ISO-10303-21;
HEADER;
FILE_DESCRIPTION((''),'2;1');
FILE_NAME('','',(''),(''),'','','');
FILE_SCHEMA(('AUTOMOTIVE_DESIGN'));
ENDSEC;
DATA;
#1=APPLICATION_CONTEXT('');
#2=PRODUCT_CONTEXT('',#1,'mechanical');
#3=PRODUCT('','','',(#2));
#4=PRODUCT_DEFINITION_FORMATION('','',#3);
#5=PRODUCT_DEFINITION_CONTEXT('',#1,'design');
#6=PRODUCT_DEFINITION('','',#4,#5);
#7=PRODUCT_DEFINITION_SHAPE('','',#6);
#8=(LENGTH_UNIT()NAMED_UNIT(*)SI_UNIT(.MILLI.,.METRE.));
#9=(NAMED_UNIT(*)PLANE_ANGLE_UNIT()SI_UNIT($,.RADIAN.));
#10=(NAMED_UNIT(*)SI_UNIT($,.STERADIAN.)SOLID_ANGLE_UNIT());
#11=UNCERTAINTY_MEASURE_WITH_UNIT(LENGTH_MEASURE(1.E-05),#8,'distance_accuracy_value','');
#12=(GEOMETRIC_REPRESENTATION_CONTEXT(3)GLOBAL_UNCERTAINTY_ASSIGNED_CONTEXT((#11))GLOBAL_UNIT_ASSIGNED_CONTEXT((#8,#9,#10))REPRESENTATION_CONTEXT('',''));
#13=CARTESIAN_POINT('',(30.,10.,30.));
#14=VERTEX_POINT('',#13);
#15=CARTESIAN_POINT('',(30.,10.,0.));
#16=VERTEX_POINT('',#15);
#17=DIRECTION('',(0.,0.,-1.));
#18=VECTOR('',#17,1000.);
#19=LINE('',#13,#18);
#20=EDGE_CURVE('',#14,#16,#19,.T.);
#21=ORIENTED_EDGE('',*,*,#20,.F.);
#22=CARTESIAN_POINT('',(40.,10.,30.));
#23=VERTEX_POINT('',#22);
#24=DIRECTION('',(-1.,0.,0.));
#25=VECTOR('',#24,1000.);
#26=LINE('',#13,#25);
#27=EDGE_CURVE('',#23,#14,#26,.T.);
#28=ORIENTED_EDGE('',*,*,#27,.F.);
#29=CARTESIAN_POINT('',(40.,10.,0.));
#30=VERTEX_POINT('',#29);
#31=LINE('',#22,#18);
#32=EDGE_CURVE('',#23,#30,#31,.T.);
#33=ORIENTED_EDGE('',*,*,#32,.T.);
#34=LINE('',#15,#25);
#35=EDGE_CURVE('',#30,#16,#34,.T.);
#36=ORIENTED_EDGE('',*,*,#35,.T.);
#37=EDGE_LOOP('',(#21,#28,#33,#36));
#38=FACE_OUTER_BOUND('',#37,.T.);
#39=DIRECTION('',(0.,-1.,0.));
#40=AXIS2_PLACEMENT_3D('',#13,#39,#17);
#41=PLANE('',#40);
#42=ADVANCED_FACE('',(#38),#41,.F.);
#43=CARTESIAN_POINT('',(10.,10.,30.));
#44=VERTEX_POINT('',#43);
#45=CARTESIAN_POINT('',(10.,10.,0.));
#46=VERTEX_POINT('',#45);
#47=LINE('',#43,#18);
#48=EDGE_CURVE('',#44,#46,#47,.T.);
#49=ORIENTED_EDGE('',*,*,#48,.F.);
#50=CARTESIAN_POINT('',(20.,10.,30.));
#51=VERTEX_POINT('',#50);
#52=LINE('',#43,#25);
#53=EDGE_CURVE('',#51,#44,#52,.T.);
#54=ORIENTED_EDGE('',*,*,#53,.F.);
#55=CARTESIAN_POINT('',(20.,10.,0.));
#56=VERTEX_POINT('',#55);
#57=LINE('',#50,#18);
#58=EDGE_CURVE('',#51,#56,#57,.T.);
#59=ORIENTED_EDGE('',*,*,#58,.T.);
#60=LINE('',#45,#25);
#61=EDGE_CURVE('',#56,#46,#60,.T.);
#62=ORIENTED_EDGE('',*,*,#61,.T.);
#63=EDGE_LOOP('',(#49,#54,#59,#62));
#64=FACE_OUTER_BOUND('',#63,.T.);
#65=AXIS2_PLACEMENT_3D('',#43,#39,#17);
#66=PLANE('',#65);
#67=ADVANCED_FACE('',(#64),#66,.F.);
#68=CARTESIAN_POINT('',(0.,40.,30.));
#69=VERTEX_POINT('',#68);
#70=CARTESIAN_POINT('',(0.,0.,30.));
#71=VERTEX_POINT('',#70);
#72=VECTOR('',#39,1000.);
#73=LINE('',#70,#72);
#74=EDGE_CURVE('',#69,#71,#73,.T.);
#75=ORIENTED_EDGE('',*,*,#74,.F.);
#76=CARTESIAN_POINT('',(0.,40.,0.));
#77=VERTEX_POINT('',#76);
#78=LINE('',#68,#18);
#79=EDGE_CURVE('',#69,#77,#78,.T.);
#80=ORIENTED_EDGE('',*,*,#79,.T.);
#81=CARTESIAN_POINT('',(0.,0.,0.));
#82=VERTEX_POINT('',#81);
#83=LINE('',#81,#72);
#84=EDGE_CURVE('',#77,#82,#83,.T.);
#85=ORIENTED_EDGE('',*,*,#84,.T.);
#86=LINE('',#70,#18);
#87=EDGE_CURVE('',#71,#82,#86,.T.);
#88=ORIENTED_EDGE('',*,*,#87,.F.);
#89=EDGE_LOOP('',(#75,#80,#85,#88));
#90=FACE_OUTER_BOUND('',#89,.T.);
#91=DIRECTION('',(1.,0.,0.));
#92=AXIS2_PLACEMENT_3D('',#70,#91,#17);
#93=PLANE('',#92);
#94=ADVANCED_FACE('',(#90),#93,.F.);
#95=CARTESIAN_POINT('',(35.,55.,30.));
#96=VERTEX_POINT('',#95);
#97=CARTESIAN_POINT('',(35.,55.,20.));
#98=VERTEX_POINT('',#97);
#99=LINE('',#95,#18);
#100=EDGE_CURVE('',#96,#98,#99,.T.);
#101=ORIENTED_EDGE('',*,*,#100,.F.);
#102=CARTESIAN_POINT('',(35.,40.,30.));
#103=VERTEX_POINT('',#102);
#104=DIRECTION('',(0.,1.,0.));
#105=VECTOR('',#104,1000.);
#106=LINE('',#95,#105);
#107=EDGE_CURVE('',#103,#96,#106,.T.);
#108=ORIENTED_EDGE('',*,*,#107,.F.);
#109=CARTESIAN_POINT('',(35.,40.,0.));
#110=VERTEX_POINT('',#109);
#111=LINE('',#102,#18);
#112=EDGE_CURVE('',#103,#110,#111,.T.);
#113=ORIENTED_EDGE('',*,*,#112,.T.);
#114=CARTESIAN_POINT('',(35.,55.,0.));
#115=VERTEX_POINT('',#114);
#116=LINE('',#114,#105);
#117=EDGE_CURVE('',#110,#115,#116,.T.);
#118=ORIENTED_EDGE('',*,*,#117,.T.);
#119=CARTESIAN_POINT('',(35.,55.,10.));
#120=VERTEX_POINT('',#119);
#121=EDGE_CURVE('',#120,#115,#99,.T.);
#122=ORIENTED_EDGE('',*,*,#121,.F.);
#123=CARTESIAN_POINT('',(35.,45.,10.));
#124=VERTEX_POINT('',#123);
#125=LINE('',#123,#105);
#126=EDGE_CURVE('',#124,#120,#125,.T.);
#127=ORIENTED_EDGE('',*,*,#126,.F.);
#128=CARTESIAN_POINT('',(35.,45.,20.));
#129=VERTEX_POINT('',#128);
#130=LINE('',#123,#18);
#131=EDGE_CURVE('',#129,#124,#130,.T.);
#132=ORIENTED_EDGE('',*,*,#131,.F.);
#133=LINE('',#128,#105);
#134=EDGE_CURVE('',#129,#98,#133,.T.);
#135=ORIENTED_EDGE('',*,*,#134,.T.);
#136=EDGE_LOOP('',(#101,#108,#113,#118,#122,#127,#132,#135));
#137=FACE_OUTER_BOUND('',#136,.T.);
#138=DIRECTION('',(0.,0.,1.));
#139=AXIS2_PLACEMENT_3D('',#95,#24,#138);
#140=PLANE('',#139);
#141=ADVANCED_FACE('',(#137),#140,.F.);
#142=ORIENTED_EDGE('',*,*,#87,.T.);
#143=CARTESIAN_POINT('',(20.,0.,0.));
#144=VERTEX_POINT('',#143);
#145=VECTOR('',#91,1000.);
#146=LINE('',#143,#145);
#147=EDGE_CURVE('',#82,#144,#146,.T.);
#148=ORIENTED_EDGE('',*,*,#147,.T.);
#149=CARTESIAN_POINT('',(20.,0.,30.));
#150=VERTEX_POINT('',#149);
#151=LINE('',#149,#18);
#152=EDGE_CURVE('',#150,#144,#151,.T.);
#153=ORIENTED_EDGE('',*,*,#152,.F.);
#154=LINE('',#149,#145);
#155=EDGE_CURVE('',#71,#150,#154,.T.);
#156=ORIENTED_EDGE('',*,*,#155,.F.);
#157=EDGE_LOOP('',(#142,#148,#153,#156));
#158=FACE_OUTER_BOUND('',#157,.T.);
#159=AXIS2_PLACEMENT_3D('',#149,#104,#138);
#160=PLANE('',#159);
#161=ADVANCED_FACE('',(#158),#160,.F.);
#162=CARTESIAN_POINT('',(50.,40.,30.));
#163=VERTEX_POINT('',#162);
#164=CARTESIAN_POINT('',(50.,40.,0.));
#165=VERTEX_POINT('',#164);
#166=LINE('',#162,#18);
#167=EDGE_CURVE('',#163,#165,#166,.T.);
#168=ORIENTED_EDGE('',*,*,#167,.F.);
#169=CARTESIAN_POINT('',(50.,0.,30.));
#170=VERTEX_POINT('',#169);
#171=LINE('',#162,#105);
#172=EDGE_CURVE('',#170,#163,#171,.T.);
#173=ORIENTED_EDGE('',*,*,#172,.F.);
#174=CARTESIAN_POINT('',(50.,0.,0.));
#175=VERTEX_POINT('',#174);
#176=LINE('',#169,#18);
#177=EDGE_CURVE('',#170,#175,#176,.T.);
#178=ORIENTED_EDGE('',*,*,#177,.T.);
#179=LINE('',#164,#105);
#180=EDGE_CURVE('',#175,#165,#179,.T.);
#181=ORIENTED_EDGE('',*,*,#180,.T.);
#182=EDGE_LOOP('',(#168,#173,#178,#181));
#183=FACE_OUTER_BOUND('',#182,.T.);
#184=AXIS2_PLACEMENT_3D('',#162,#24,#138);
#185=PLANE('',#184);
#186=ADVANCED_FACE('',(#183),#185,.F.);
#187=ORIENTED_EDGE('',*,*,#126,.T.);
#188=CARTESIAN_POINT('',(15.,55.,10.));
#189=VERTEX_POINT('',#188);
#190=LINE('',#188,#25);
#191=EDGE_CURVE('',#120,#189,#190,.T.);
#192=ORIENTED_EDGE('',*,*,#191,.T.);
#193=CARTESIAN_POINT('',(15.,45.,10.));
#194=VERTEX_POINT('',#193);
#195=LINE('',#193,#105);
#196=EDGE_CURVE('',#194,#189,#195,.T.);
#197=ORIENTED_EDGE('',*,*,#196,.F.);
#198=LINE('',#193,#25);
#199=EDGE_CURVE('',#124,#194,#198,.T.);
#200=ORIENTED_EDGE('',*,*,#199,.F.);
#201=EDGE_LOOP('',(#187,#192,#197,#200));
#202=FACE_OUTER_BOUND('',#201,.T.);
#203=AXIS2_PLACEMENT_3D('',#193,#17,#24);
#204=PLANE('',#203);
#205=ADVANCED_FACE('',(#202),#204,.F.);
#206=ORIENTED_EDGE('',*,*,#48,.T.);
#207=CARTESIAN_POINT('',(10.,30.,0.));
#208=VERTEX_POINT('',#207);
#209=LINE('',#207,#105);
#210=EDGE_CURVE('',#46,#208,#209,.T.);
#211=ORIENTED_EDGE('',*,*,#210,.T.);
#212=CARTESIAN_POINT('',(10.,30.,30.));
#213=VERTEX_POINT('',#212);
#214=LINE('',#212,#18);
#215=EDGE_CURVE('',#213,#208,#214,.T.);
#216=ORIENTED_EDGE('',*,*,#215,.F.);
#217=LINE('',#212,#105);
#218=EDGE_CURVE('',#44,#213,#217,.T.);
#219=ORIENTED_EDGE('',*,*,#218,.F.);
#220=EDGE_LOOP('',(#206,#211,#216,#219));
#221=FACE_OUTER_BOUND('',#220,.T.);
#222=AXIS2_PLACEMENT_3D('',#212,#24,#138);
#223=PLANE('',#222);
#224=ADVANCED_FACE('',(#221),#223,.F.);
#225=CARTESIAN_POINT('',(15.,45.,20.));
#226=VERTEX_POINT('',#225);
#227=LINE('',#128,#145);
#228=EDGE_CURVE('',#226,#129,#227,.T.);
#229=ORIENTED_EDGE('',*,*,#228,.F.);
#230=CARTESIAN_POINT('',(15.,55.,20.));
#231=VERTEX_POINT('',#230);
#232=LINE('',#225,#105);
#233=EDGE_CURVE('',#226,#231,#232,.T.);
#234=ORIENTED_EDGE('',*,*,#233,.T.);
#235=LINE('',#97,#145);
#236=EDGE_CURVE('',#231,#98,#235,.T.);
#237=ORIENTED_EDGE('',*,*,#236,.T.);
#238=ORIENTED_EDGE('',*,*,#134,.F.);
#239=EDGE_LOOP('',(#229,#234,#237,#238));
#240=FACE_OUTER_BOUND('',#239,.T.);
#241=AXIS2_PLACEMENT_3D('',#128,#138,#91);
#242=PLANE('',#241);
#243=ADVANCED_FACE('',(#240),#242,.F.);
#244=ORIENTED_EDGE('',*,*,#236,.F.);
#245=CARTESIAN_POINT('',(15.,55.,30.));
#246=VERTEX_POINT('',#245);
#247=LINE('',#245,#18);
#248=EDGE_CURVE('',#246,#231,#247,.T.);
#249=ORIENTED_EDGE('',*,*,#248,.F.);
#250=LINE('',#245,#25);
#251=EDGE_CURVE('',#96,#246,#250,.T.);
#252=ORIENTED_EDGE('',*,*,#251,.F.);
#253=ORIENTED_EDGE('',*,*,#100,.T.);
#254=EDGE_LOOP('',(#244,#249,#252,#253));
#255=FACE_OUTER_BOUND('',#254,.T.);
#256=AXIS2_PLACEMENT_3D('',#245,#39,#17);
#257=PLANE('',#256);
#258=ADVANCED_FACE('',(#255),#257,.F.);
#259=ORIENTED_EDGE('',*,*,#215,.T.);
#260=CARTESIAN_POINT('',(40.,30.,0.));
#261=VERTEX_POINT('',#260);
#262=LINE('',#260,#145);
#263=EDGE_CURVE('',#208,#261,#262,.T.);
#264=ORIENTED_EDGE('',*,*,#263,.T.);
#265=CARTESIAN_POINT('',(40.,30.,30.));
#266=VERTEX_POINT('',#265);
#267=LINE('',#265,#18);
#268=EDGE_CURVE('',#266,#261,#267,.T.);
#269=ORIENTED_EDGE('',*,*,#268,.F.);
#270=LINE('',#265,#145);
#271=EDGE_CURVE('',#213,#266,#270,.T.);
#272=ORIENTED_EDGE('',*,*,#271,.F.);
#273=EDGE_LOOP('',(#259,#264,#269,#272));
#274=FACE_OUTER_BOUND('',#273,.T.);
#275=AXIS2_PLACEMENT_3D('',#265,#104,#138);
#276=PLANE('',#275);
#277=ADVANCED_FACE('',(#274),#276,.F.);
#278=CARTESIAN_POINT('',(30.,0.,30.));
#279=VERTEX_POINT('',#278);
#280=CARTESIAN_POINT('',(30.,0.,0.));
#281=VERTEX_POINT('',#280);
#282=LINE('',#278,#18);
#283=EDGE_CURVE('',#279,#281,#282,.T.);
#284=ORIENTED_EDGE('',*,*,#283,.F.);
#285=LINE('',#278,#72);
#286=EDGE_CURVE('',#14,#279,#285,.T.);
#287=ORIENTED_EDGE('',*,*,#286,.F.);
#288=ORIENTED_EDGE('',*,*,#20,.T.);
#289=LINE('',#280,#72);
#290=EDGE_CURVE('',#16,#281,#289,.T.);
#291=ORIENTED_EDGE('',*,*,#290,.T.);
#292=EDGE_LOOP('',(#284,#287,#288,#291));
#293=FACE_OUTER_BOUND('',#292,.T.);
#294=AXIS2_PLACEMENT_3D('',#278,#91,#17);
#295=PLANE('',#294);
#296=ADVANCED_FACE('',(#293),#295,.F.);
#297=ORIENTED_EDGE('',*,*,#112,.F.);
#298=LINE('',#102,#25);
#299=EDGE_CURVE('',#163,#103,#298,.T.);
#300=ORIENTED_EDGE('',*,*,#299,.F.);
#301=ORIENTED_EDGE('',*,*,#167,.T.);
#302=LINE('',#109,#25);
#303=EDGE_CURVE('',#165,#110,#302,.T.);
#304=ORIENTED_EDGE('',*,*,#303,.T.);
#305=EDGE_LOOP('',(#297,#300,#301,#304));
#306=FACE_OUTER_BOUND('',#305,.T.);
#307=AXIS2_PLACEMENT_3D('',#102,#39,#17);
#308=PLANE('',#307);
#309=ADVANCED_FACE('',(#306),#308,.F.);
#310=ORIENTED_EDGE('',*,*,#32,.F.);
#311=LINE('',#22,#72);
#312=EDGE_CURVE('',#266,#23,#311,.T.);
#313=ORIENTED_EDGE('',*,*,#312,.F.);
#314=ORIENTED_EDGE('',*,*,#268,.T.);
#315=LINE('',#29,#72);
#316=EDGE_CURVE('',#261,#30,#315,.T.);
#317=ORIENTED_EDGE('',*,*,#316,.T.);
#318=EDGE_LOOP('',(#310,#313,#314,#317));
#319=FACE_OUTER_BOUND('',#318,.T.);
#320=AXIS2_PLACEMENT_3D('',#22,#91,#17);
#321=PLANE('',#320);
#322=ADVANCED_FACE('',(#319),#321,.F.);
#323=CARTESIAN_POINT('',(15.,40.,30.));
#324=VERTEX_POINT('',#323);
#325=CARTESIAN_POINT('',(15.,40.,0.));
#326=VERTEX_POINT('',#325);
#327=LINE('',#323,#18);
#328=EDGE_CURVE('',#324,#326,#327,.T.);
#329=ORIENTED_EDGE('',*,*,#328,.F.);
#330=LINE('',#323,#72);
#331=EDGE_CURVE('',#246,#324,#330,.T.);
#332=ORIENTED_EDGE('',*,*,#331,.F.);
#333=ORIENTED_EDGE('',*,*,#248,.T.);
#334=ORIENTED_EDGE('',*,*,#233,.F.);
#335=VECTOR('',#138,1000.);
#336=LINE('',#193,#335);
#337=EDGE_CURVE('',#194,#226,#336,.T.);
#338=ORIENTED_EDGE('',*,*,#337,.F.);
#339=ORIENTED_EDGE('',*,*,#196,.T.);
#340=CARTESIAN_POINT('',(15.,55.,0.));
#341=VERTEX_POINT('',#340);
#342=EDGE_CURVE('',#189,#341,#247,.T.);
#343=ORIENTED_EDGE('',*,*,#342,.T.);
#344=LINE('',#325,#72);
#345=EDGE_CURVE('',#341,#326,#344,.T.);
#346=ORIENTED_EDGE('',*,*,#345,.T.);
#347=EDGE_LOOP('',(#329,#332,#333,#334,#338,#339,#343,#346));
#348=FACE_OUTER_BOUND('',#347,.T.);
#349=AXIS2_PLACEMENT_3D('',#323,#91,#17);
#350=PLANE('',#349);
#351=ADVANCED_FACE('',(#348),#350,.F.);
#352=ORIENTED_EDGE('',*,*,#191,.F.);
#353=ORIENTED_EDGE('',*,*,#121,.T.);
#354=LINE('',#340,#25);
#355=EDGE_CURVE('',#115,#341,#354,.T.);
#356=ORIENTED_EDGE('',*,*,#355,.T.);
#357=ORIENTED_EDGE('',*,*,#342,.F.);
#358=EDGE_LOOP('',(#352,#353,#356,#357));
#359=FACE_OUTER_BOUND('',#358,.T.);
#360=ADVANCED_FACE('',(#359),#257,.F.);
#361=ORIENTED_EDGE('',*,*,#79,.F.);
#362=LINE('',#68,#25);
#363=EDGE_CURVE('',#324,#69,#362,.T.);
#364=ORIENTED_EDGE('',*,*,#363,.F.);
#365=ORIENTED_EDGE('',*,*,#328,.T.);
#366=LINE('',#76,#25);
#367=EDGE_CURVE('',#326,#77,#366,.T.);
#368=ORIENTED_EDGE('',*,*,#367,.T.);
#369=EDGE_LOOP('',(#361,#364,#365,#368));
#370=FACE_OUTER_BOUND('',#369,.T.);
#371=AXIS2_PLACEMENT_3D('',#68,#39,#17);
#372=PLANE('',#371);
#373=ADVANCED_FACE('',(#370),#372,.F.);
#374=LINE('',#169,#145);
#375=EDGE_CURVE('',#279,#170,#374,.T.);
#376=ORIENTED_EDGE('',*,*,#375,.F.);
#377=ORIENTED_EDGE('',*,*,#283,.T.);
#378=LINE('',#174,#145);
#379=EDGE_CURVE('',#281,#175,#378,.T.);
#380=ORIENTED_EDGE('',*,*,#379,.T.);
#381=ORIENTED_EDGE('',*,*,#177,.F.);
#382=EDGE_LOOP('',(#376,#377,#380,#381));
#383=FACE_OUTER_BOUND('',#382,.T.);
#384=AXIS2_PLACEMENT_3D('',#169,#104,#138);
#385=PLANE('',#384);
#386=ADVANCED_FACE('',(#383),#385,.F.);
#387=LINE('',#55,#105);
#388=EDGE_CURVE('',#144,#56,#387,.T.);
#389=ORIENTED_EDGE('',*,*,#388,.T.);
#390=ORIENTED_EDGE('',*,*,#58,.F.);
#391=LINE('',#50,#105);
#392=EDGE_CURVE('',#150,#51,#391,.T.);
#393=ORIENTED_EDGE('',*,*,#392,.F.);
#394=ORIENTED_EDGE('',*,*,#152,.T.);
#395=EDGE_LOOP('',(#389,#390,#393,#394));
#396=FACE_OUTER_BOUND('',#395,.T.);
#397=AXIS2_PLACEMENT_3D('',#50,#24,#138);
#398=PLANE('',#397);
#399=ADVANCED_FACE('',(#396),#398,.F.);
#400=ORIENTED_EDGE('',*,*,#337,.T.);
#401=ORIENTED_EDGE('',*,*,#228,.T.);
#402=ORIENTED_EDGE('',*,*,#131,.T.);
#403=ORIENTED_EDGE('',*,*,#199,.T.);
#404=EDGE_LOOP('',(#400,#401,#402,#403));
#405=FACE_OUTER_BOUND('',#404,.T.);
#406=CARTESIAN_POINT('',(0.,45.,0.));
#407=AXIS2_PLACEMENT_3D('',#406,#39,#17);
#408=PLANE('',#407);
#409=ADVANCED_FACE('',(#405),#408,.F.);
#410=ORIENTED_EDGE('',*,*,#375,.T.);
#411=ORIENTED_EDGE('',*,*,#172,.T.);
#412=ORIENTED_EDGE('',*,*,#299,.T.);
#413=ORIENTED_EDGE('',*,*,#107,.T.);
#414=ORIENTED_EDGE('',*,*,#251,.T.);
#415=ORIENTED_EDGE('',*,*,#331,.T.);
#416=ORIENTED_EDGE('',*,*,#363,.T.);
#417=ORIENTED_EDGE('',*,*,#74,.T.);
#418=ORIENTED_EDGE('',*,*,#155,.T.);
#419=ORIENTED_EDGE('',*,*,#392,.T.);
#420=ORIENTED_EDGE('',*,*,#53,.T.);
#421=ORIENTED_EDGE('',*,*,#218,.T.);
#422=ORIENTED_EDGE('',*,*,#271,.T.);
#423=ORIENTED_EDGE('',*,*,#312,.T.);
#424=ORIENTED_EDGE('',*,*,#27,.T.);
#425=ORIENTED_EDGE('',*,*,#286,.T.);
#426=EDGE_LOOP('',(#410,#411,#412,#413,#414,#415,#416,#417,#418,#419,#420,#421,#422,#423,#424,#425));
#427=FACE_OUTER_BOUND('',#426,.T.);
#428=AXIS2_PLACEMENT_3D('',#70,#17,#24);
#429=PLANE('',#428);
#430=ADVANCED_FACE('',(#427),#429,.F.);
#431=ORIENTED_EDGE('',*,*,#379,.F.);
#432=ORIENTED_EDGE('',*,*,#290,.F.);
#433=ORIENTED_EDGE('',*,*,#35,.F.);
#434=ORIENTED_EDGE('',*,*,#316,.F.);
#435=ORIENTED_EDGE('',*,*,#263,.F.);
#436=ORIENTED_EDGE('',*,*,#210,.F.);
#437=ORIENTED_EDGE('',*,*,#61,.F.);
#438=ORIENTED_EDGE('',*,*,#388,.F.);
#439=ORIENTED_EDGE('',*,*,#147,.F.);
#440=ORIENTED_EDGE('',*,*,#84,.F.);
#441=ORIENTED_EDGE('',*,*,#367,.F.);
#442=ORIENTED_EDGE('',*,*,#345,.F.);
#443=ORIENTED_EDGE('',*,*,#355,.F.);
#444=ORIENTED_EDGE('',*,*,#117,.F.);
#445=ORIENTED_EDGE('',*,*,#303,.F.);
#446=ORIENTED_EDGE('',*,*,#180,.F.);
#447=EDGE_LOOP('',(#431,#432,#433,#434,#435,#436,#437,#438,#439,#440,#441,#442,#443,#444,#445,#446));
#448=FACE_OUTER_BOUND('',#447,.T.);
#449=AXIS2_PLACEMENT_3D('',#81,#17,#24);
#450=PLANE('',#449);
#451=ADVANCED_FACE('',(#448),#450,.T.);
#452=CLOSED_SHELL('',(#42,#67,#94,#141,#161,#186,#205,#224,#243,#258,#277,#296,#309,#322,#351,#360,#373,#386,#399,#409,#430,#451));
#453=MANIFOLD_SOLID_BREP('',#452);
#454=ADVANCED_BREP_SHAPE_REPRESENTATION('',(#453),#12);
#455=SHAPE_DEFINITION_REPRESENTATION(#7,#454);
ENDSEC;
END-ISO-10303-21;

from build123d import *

# Parameters (mm, degrees)
BLOCK_BODY_EXTRUDE_30MM_DEPTH = 30
POCKET_SKETCH_W               = 20
POCKET_SKETCH_H               = 10
POCKET_CUT_10MM_DEPTH         = 10


with BuildPart() as part:
    # Block Profile Sketch → Block Body Extrude 30mm (new body)
    with BuildSketch(Plane.XY):
        Polygon((0, 0), (0, 40), (15, 40), (15, 55), (35, 55), (35, 40), (50, 40), (50, 0), (30, 0), (30, 10), (40, 10), (40, 30), (10, 30), (10, 10), (20, 10), (20, 0), align=None)
    extrude(amount=BLOCK_BODY_EXTRUDE_30MM_DEPTH)

    # Pocket Sketch → Pocket Cut 10mm (cut)
    with BuildSketch(Plane(origin=(0, 55, 0), x_dir=(1, 0, 0), z_dir=(0, 1, 0))):
        with Locations((25, -15)):
            Rectangle(POCKET_SKETCH_W, POCKET_SKETCH_H)
    extrude(amount=-POCKET_CUT_10MM_DEPTH, mode=Mode.SUBTRACT)


solid = part.part
